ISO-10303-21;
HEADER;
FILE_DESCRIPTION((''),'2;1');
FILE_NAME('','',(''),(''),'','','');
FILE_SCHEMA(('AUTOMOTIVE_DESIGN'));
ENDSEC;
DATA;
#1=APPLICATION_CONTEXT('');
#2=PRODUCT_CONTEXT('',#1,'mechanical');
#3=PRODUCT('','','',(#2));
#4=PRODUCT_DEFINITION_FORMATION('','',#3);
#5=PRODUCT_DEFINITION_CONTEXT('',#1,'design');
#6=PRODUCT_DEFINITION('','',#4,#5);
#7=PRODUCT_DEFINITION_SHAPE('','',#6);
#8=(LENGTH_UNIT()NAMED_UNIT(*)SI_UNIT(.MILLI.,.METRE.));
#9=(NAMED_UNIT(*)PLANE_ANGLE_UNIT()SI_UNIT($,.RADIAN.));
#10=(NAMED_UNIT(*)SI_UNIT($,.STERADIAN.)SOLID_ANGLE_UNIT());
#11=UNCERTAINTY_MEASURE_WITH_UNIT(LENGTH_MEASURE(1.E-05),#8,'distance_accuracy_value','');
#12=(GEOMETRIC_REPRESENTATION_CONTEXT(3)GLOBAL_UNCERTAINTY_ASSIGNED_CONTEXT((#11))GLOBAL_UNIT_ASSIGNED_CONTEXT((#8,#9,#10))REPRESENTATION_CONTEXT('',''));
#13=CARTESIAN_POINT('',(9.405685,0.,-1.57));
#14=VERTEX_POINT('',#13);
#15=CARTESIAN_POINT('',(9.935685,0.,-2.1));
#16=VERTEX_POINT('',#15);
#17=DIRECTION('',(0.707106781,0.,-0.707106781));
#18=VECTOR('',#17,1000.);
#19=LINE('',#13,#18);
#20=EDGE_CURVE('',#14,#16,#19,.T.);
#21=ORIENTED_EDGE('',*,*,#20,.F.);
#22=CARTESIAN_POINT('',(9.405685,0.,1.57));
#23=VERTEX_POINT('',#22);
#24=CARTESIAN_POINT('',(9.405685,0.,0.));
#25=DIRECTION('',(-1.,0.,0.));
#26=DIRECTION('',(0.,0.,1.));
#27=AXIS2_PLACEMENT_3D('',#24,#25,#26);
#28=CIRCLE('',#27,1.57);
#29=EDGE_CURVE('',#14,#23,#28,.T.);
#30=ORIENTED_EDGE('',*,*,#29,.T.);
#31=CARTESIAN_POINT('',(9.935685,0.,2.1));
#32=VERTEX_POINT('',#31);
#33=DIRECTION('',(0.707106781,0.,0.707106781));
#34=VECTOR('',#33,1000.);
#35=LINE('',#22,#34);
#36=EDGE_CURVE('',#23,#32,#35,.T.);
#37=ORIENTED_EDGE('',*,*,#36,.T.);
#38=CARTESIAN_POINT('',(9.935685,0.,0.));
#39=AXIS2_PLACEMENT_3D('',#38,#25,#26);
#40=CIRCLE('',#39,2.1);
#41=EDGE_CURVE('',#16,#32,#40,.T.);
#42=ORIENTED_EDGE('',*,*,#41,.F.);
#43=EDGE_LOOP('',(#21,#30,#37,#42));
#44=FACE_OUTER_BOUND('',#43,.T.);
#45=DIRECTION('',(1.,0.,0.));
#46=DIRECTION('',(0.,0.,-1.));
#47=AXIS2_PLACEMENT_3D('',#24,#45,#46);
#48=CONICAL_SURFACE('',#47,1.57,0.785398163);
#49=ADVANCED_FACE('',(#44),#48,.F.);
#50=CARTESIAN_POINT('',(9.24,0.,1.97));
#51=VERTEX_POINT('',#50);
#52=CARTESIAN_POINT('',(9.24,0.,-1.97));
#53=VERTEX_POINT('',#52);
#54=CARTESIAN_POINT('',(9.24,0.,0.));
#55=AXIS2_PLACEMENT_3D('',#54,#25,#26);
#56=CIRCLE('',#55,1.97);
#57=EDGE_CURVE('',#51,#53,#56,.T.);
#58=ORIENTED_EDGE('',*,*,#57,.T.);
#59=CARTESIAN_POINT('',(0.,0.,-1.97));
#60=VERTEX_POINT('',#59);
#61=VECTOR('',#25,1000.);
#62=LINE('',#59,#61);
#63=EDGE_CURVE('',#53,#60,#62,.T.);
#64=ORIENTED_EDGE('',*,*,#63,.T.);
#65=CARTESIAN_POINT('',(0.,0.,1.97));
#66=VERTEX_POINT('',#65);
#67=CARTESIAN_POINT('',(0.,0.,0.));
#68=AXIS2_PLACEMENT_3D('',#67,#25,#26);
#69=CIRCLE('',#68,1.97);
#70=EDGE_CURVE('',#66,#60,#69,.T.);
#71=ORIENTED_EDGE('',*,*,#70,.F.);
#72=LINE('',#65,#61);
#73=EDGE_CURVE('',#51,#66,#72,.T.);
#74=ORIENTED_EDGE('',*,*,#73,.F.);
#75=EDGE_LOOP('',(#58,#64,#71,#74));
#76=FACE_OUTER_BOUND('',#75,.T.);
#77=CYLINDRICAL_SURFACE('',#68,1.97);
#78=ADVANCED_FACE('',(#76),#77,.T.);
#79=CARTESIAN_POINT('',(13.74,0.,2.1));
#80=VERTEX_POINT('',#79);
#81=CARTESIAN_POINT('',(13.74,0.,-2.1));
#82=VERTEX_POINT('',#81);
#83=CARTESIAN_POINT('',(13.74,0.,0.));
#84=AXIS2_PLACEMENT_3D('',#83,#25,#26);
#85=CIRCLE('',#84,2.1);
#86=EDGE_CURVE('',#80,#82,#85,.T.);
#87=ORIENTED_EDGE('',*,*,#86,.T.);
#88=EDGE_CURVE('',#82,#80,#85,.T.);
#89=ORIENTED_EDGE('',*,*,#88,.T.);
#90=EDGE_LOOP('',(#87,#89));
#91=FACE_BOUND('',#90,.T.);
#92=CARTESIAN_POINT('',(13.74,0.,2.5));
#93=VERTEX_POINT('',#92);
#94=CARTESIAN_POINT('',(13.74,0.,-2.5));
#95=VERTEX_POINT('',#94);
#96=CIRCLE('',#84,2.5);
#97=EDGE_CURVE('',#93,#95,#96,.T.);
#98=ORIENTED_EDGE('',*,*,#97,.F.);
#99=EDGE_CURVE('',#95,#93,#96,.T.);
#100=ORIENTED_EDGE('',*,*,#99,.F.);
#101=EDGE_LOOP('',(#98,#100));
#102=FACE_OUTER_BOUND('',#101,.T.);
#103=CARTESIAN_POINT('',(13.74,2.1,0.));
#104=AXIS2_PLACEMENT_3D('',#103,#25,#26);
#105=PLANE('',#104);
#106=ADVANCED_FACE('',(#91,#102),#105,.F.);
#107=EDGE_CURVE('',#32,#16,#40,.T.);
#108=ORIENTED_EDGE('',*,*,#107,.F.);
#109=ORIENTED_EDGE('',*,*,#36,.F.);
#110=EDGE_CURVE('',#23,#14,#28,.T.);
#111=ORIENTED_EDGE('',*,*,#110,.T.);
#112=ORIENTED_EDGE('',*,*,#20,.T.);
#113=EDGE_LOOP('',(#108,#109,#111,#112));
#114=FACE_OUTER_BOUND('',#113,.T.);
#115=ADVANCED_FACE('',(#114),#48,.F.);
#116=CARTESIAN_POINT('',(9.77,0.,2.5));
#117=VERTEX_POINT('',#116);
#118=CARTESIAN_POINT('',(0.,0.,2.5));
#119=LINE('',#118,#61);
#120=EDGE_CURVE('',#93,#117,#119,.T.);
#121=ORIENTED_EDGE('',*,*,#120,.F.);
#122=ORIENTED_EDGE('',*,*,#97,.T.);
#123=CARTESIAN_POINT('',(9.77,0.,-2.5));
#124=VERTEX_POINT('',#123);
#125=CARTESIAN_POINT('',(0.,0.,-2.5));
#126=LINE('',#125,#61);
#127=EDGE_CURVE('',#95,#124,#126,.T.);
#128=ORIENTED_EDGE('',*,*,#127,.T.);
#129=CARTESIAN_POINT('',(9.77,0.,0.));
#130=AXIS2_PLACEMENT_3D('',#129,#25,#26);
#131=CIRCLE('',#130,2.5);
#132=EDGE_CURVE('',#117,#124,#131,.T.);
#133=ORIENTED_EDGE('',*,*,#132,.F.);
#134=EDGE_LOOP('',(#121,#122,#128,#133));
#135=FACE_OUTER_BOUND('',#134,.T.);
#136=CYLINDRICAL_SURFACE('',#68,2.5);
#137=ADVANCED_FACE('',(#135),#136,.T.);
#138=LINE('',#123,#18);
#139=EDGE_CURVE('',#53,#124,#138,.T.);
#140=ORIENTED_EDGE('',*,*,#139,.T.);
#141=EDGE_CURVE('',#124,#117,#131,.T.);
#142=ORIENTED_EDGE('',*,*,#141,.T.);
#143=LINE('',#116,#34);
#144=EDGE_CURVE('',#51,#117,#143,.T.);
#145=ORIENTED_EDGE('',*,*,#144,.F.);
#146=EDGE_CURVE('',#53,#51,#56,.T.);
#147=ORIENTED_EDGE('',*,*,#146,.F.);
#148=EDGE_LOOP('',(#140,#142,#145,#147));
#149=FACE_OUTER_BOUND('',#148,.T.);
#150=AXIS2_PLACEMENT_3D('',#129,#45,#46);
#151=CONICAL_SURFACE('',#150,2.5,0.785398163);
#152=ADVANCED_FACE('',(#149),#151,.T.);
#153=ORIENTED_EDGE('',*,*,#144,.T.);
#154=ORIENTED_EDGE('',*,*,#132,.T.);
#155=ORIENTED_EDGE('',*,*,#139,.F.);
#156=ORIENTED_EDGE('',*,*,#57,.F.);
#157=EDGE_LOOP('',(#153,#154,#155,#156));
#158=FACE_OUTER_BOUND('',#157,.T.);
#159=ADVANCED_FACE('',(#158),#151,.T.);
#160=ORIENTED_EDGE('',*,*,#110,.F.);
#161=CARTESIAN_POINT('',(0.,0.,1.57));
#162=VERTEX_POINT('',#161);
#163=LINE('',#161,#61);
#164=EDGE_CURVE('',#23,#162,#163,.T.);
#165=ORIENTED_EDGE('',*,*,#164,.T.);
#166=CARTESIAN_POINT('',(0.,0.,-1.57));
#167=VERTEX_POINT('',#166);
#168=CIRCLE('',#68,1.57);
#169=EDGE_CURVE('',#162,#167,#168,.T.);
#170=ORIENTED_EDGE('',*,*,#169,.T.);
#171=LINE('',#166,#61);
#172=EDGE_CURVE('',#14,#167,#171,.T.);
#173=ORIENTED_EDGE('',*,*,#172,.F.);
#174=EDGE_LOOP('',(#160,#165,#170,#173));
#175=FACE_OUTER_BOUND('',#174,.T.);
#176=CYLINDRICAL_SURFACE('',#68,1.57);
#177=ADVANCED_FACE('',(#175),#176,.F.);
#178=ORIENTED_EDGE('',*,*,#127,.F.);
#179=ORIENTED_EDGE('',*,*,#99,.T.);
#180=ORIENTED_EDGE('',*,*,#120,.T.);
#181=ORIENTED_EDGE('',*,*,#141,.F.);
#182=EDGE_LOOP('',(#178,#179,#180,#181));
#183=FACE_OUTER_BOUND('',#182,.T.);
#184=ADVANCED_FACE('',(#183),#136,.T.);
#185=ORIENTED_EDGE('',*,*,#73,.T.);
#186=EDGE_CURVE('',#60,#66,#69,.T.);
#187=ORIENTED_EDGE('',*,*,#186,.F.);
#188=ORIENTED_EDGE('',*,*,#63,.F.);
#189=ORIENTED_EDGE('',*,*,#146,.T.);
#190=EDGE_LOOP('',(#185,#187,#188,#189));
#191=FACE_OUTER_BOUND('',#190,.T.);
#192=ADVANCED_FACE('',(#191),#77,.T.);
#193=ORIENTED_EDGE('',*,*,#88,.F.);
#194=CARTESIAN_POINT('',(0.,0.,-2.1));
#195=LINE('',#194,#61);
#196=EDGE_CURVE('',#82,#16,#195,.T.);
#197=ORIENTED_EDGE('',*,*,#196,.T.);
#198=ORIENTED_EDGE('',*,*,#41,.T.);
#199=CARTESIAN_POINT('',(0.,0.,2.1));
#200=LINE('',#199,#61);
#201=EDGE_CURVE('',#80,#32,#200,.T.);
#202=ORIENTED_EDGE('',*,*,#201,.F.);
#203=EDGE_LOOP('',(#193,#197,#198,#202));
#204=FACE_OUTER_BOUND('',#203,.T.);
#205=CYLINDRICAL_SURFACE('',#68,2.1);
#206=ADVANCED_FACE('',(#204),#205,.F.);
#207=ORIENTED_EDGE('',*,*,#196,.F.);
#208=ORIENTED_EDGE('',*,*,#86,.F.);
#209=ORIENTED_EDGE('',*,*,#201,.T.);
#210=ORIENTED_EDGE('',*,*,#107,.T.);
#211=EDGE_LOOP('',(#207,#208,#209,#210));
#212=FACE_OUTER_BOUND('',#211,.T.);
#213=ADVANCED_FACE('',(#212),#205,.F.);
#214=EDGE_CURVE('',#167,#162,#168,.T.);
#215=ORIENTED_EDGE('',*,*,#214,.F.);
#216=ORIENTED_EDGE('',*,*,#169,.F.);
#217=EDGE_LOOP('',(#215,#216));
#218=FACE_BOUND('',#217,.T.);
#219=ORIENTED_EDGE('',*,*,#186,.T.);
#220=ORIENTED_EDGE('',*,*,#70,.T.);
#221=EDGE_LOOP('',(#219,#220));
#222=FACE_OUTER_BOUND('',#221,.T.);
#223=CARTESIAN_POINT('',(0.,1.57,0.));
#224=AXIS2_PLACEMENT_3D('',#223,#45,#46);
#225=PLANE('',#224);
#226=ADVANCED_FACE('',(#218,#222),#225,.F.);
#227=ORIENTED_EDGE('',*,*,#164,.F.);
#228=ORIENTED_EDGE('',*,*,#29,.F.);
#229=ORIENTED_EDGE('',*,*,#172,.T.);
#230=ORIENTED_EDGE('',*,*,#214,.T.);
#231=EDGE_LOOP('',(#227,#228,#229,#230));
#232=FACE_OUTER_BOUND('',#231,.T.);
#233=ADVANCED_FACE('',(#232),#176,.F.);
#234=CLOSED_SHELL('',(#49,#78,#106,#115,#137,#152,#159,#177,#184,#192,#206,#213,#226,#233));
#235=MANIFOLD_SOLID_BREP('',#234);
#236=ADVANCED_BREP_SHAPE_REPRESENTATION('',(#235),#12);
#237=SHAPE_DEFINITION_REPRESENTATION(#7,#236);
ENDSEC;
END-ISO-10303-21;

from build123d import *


with BuildPart() as part:
    # Sketch1 → Revolve1 (revolve)
    with BuildSketch(Plane.XY, mode=Mode.PRIVATE) as revolve1_sk:
        Polygon((0, 1.97), (9.24, 1.97), (9.77, 2.5), (13.74, 2.5), (13.74, 2.1), (9.935685425, 2.1), (9.405685425, 1.57), (0, 1.57), align=None)
    revolve(revolve1_sk.sketch.rotate(Axis((0, 0, 0), (1, 0, 0)), 90), axis=Axis((0, 0, 0), (1, 0, 0)))


solid = part.part
